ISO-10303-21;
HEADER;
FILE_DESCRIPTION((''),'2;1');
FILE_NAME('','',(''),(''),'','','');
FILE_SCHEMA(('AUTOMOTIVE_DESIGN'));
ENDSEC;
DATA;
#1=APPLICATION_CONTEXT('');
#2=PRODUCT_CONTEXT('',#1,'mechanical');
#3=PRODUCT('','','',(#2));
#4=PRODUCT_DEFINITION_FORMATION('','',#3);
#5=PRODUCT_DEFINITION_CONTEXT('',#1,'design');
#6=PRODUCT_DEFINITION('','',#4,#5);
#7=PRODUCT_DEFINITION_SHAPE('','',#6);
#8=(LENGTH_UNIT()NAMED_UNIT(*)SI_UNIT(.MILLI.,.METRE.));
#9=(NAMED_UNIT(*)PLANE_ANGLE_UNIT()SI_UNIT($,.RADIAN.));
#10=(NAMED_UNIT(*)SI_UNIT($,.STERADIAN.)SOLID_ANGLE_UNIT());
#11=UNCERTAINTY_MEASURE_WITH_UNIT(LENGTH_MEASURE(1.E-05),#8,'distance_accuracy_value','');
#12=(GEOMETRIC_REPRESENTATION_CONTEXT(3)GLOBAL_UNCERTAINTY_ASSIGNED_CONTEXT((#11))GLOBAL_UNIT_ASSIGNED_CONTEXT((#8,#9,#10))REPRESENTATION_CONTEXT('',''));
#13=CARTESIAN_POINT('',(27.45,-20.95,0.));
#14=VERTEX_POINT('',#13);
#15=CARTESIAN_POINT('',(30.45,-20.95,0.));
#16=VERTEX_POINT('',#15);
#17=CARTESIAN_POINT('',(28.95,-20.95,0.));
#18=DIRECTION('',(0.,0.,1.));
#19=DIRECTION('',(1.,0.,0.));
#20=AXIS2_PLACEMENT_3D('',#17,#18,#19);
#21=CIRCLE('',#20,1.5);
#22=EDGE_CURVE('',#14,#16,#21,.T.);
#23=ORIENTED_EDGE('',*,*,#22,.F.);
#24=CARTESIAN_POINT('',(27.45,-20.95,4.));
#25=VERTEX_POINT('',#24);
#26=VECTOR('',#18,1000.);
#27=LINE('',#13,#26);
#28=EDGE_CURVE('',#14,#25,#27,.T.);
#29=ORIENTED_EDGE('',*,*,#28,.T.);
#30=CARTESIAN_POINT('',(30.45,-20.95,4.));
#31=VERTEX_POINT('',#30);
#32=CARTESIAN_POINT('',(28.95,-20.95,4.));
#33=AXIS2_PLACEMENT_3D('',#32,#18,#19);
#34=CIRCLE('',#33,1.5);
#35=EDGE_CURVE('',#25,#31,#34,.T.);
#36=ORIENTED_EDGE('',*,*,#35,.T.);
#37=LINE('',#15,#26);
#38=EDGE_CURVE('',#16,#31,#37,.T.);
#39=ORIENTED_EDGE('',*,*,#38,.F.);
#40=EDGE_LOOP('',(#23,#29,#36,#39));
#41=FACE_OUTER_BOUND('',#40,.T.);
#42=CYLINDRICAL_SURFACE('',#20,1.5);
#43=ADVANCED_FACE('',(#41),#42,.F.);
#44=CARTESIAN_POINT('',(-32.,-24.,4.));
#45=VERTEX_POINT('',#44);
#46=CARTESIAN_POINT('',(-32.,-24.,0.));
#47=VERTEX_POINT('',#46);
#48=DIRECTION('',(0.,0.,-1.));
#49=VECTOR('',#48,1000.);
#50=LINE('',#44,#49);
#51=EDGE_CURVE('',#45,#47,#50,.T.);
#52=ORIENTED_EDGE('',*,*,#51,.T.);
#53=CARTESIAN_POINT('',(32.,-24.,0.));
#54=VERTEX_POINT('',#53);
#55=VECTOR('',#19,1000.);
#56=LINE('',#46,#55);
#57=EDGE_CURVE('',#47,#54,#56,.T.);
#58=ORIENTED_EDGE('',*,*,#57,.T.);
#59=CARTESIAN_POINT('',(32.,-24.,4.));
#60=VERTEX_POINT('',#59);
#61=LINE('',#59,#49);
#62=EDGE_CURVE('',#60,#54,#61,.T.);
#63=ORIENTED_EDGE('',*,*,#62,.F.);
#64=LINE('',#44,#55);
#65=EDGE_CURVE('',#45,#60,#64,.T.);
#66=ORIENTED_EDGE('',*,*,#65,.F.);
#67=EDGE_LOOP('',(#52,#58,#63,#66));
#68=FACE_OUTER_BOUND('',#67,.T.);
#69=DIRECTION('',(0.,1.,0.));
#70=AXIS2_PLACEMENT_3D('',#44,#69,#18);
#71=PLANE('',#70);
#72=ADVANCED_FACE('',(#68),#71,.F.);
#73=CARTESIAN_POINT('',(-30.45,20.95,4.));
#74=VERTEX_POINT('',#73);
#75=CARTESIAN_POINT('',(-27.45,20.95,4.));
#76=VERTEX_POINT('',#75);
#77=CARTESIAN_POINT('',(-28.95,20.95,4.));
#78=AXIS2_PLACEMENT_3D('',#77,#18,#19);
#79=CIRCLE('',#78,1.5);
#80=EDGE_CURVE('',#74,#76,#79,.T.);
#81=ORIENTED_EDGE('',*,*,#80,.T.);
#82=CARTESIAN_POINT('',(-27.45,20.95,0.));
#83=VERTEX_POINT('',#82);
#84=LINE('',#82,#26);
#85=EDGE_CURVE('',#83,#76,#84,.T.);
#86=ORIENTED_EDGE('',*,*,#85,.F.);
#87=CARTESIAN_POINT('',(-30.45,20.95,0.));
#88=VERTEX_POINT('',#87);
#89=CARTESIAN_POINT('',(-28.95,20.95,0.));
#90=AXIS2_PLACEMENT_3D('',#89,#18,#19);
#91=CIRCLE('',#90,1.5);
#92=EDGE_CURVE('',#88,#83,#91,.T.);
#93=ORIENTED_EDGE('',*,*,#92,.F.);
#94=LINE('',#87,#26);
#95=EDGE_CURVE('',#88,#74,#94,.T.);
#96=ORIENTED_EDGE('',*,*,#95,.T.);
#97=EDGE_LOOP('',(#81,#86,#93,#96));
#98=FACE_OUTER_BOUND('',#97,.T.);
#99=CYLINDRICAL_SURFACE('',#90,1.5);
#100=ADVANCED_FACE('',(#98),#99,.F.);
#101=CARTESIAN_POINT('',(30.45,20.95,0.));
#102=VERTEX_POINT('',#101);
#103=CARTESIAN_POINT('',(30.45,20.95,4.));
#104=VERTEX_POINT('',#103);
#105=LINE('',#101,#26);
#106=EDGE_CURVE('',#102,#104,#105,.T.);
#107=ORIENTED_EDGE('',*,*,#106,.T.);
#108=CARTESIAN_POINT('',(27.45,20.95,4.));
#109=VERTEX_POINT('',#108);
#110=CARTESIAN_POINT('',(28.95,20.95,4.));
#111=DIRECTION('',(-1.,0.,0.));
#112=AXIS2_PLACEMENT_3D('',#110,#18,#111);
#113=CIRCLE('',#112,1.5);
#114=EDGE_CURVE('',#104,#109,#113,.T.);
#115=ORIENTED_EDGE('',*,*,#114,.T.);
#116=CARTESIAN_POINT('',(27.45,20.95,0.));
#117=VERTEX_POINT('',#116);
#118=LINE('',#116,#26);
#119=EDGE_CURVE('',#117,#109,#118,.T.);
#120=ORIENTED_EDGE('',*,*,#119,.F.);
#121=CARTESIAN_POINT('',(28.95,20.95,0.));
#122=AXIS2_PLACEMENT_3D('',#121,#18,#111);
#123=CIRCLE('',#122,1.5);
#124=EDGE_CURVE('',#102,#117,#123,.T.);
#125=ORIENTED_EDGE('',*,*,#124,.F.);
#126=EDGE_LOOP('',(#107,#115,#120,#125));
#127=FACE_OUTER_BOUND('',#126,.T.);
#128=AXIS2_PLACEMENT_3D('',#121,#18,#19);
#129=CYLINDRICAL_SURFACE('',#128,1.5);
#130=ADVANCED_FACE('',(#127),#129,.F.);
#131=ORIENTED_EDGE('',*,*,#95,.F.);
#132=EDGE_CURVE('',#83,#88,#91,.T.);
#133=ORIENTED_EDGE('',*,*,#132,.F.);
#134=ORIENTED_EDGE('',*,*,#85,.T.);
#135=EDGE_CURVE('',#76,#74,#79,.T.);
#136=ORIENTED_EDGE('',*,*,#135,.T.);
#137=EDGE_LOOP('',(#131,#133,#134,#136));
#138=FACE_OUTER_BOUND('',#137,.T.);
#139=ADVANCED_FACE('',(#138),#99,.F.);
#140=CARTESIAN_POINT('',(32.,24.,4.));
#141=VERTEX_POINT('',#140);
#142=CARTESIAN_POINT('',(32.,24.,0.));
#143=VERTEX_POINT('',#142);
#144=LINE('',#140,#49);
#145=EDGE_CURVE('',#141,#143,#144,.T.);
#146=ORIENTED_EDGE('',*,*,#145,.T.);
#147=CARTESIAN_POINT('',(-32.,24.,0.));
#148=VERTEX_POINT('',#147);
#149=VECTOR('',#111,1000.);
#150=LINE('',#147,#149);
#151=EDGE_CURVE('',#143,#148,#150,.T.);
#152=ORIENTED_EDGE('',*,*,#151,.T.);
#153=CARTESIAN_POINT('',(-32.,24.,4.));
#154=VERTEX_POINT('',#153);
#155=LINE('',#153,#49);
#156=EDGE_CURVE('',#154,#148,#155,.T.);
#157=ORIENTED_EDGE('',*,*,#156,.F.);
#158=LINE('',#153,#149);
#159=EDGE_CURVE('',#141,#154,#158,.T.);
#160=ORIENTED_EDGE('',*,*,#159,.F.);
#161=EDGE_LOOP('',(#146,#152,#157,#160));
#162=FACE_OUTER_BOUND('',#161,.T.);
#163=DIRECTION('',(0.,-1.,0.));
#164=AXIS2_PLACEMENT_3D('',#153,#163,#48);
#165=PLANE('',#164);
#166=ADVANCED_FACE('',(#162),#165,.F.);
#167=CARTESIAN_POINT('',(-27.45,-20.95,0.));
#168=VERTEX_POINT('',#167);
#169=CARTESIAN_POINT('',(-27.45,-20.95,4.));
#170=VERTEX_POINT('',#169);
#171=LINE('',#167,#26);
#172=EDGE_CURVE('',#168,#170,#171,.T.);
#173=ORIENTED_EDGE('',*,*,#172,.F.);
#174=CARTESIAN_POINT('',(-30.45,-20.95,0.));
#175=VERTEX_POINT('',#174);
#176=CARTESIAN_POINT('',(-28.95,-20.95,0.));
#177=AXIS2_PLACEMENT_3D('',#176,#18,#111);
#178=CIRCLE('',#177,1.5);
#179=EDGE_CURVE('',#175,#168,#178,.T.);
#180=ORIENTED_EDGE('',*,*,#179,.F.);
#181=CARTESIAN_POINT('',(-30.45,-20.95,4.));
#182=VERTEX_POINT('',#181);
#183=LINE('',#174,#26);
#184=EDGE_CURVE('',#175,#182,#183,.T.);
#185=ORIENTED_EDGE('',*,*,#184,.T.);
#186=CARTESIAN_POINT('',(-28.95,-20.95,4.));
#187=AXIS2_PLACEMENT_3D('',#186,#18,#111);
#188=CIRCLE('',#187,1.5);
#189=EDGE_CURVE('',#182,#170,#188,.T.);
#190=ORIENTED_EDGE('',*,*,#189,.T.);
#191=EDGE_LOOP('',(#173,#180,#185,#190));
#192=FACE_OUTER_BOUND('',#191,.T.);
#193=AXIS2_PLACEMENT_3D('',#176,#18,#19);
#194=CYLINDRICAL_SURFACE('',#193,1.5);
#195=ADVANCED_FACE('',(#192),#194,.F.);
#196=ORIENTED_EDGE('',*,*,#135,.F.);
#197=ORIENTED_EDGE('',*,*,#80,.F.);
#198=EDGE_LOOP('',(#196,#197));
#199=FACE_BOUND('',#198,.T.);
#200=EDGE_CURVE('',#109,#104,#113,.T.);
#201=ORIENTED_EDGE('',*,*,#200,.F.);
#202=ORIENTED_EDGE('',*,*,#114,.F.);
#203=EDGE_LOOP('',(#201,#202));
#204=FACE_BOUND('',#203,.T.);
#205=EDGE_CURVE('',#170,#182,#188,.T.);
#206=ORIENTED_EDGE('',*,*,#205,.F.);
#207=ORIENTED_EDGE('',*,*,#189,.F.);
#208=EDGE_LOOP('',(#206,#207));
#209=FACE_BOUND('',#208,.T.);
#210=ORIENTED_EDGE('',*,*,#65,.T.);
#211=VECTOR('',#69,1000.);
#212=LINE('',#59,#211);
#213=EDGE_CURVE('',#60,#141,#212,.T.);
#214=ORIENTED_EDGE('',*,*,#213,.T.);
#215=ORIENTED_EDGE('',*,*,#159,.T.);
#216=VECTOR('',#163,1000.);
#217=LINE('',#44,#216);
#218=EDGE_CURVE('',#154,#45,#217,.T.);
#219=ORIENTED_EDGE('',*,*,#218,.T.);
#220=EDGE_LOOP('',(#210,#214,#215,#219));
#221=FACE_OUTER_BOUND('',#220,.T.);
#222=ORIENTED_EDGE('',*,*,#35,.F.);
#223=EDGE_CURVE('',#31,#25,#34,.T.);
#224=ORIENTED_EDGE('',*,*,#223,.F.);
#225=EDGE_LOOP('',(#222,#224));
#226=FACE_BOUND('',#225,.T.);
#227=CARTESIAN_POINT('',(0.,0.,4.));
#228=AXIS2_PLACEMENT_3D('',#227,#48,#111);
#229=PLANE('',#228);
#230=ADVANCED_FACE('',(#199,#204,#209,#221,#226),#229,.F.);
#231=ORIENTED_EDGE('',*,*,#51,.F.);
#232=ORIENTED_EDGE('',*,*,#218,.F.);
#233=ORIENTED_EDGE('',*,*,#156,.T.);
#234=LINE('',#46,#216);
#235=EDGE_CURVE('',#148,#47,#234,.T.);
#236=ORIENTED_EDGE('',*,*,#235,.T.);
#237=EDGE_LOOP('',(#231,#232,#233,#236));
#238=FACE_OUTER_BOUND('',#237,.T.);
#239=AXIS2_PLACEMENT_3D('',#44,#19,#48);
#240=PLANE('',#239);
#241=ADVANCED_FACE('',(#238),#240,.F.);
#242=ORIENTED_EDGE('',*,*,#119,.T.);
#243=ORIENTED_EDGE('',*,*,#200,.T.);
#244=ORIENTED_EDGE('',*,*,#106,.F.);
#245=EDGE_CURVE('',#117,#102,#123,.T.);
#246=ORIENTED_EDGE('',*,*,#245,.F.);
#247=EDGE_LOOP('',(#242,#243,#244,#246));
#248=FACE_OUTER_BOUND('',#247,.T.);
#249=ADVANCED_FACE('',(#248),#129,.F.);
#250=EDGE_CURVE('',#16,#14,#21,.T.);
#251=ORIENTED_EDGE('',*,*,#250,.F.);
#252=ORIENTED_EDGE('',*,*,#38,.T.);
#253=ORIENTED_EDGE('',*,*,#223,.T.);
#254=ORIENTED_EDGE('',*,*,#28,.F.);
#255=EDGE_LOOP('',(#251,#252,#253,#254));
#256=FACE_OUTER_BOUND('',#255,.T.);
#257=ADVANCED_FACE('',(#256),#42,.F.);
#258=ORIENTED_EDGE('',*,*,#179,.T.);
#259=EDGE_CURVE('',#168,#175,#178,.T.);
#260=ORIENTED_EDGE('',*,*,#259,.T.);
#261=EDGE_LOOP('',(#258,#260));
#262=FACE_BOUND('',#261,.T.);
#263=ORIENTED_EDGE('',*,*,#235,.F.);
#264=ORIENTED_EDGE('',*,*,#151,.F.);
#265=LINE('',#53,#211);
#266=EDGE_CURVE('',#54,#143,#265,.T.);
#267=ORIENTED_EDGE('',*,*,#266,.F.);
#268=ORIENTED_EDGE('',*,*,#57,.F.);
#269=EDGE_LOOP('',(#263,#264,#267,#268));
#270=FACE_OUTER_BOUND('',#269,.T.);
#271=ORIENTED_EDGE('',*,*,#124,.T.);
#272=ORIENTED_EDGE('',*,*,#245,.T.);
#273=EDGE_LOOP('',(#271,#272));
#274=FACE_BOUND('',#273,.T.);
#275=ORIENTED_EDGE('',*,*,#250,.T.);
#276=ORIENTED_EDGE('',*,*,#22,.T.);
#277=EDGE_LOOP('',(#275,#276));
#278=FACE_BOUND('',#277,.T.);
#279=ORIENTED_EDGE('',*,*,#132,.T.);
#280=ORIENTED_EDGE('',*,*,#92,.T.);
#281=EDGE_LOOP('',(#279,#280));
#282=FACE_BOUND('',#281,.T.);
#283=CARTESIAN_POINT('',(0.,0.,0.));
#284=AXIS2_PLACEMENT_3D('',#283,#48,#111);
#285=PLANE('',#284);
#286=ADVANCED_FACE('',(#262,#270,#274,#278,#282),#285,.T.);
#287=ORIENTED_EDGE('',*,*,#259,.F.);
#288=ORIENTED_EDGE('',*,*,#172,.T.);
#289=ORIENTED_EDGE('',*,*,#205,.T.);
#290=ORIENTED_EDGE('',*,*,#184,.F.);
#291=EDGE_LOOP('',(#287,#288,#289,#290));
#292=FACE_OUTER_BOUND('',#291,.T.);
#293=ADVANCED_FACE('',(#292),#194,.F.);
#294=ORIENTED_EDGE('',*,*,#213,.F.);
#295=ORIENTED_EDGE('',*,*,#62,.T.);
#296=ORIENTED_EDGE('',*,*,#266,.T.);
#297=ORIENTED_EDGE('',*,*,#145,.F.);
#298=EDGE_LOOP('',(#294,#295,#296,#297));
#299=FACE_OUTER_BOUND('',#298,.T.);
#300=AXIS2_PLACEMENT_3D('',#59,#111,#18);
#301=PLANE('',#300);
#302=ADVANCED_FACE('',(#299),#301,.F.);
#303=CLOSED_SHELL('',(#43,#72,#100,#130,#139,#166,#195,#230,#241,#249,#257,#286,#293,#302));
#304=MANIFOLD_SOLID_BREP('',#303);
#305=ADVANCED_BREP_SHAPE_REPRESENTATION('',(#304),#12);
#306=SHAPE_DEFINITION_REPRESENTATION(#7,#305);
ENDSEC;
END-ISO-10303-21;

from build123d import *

# Parameters (mm, degrees)
SKETCH1_W               = 64
SKETCH1_H               = 48
BOSS_EXTRUDE1_DEPTH     = 4
CUT_EXTRUDE1_DEPTH      = 41.199502484
CUT_EXTRUDE1_DEPTH_BACK = 41.199502484
SKETCH2_R               = 1.5


with BuildPart() as part:
    # Sketch1 → Boss-Extrude1 (new body)
    with BuildSketch(Plane.XY):
        Rectangle(SKETCH1_W, SKETCH1_H)
    extrude(amount=BOSS_EXTRUDE1_DEPTH)

    # Sketch2 → Cut-Extrude1 (cut, two sides: drawn at the far end of the back side and taken through both)
    with BuildSketch(Plane.XY.offset(4).offset(-CUT_EXTRUDE1_DEPTH_BACK)):
        with Locations((28.95, -20.95)):
            Circle(SKETCH2_R)
        with Locations(Location((-28.95, -20.95, 0), (0, 0, 180))):
            Circle(SKETCH2_R)
        with Locations(Location((28.95, 20.95, 0), (0, 0, 180))):
            Circle(SKETCH2_R)
        with Locations((-28.95, 20.95)):
            Circle(SKETCH2_R)
    extrude(amount=CUT_EXTRUDE1_DEPTH + CUT_EXTRUDE1_DEPTH_BACK, mode=Mode.SUBTRACT)


solid = part.part
